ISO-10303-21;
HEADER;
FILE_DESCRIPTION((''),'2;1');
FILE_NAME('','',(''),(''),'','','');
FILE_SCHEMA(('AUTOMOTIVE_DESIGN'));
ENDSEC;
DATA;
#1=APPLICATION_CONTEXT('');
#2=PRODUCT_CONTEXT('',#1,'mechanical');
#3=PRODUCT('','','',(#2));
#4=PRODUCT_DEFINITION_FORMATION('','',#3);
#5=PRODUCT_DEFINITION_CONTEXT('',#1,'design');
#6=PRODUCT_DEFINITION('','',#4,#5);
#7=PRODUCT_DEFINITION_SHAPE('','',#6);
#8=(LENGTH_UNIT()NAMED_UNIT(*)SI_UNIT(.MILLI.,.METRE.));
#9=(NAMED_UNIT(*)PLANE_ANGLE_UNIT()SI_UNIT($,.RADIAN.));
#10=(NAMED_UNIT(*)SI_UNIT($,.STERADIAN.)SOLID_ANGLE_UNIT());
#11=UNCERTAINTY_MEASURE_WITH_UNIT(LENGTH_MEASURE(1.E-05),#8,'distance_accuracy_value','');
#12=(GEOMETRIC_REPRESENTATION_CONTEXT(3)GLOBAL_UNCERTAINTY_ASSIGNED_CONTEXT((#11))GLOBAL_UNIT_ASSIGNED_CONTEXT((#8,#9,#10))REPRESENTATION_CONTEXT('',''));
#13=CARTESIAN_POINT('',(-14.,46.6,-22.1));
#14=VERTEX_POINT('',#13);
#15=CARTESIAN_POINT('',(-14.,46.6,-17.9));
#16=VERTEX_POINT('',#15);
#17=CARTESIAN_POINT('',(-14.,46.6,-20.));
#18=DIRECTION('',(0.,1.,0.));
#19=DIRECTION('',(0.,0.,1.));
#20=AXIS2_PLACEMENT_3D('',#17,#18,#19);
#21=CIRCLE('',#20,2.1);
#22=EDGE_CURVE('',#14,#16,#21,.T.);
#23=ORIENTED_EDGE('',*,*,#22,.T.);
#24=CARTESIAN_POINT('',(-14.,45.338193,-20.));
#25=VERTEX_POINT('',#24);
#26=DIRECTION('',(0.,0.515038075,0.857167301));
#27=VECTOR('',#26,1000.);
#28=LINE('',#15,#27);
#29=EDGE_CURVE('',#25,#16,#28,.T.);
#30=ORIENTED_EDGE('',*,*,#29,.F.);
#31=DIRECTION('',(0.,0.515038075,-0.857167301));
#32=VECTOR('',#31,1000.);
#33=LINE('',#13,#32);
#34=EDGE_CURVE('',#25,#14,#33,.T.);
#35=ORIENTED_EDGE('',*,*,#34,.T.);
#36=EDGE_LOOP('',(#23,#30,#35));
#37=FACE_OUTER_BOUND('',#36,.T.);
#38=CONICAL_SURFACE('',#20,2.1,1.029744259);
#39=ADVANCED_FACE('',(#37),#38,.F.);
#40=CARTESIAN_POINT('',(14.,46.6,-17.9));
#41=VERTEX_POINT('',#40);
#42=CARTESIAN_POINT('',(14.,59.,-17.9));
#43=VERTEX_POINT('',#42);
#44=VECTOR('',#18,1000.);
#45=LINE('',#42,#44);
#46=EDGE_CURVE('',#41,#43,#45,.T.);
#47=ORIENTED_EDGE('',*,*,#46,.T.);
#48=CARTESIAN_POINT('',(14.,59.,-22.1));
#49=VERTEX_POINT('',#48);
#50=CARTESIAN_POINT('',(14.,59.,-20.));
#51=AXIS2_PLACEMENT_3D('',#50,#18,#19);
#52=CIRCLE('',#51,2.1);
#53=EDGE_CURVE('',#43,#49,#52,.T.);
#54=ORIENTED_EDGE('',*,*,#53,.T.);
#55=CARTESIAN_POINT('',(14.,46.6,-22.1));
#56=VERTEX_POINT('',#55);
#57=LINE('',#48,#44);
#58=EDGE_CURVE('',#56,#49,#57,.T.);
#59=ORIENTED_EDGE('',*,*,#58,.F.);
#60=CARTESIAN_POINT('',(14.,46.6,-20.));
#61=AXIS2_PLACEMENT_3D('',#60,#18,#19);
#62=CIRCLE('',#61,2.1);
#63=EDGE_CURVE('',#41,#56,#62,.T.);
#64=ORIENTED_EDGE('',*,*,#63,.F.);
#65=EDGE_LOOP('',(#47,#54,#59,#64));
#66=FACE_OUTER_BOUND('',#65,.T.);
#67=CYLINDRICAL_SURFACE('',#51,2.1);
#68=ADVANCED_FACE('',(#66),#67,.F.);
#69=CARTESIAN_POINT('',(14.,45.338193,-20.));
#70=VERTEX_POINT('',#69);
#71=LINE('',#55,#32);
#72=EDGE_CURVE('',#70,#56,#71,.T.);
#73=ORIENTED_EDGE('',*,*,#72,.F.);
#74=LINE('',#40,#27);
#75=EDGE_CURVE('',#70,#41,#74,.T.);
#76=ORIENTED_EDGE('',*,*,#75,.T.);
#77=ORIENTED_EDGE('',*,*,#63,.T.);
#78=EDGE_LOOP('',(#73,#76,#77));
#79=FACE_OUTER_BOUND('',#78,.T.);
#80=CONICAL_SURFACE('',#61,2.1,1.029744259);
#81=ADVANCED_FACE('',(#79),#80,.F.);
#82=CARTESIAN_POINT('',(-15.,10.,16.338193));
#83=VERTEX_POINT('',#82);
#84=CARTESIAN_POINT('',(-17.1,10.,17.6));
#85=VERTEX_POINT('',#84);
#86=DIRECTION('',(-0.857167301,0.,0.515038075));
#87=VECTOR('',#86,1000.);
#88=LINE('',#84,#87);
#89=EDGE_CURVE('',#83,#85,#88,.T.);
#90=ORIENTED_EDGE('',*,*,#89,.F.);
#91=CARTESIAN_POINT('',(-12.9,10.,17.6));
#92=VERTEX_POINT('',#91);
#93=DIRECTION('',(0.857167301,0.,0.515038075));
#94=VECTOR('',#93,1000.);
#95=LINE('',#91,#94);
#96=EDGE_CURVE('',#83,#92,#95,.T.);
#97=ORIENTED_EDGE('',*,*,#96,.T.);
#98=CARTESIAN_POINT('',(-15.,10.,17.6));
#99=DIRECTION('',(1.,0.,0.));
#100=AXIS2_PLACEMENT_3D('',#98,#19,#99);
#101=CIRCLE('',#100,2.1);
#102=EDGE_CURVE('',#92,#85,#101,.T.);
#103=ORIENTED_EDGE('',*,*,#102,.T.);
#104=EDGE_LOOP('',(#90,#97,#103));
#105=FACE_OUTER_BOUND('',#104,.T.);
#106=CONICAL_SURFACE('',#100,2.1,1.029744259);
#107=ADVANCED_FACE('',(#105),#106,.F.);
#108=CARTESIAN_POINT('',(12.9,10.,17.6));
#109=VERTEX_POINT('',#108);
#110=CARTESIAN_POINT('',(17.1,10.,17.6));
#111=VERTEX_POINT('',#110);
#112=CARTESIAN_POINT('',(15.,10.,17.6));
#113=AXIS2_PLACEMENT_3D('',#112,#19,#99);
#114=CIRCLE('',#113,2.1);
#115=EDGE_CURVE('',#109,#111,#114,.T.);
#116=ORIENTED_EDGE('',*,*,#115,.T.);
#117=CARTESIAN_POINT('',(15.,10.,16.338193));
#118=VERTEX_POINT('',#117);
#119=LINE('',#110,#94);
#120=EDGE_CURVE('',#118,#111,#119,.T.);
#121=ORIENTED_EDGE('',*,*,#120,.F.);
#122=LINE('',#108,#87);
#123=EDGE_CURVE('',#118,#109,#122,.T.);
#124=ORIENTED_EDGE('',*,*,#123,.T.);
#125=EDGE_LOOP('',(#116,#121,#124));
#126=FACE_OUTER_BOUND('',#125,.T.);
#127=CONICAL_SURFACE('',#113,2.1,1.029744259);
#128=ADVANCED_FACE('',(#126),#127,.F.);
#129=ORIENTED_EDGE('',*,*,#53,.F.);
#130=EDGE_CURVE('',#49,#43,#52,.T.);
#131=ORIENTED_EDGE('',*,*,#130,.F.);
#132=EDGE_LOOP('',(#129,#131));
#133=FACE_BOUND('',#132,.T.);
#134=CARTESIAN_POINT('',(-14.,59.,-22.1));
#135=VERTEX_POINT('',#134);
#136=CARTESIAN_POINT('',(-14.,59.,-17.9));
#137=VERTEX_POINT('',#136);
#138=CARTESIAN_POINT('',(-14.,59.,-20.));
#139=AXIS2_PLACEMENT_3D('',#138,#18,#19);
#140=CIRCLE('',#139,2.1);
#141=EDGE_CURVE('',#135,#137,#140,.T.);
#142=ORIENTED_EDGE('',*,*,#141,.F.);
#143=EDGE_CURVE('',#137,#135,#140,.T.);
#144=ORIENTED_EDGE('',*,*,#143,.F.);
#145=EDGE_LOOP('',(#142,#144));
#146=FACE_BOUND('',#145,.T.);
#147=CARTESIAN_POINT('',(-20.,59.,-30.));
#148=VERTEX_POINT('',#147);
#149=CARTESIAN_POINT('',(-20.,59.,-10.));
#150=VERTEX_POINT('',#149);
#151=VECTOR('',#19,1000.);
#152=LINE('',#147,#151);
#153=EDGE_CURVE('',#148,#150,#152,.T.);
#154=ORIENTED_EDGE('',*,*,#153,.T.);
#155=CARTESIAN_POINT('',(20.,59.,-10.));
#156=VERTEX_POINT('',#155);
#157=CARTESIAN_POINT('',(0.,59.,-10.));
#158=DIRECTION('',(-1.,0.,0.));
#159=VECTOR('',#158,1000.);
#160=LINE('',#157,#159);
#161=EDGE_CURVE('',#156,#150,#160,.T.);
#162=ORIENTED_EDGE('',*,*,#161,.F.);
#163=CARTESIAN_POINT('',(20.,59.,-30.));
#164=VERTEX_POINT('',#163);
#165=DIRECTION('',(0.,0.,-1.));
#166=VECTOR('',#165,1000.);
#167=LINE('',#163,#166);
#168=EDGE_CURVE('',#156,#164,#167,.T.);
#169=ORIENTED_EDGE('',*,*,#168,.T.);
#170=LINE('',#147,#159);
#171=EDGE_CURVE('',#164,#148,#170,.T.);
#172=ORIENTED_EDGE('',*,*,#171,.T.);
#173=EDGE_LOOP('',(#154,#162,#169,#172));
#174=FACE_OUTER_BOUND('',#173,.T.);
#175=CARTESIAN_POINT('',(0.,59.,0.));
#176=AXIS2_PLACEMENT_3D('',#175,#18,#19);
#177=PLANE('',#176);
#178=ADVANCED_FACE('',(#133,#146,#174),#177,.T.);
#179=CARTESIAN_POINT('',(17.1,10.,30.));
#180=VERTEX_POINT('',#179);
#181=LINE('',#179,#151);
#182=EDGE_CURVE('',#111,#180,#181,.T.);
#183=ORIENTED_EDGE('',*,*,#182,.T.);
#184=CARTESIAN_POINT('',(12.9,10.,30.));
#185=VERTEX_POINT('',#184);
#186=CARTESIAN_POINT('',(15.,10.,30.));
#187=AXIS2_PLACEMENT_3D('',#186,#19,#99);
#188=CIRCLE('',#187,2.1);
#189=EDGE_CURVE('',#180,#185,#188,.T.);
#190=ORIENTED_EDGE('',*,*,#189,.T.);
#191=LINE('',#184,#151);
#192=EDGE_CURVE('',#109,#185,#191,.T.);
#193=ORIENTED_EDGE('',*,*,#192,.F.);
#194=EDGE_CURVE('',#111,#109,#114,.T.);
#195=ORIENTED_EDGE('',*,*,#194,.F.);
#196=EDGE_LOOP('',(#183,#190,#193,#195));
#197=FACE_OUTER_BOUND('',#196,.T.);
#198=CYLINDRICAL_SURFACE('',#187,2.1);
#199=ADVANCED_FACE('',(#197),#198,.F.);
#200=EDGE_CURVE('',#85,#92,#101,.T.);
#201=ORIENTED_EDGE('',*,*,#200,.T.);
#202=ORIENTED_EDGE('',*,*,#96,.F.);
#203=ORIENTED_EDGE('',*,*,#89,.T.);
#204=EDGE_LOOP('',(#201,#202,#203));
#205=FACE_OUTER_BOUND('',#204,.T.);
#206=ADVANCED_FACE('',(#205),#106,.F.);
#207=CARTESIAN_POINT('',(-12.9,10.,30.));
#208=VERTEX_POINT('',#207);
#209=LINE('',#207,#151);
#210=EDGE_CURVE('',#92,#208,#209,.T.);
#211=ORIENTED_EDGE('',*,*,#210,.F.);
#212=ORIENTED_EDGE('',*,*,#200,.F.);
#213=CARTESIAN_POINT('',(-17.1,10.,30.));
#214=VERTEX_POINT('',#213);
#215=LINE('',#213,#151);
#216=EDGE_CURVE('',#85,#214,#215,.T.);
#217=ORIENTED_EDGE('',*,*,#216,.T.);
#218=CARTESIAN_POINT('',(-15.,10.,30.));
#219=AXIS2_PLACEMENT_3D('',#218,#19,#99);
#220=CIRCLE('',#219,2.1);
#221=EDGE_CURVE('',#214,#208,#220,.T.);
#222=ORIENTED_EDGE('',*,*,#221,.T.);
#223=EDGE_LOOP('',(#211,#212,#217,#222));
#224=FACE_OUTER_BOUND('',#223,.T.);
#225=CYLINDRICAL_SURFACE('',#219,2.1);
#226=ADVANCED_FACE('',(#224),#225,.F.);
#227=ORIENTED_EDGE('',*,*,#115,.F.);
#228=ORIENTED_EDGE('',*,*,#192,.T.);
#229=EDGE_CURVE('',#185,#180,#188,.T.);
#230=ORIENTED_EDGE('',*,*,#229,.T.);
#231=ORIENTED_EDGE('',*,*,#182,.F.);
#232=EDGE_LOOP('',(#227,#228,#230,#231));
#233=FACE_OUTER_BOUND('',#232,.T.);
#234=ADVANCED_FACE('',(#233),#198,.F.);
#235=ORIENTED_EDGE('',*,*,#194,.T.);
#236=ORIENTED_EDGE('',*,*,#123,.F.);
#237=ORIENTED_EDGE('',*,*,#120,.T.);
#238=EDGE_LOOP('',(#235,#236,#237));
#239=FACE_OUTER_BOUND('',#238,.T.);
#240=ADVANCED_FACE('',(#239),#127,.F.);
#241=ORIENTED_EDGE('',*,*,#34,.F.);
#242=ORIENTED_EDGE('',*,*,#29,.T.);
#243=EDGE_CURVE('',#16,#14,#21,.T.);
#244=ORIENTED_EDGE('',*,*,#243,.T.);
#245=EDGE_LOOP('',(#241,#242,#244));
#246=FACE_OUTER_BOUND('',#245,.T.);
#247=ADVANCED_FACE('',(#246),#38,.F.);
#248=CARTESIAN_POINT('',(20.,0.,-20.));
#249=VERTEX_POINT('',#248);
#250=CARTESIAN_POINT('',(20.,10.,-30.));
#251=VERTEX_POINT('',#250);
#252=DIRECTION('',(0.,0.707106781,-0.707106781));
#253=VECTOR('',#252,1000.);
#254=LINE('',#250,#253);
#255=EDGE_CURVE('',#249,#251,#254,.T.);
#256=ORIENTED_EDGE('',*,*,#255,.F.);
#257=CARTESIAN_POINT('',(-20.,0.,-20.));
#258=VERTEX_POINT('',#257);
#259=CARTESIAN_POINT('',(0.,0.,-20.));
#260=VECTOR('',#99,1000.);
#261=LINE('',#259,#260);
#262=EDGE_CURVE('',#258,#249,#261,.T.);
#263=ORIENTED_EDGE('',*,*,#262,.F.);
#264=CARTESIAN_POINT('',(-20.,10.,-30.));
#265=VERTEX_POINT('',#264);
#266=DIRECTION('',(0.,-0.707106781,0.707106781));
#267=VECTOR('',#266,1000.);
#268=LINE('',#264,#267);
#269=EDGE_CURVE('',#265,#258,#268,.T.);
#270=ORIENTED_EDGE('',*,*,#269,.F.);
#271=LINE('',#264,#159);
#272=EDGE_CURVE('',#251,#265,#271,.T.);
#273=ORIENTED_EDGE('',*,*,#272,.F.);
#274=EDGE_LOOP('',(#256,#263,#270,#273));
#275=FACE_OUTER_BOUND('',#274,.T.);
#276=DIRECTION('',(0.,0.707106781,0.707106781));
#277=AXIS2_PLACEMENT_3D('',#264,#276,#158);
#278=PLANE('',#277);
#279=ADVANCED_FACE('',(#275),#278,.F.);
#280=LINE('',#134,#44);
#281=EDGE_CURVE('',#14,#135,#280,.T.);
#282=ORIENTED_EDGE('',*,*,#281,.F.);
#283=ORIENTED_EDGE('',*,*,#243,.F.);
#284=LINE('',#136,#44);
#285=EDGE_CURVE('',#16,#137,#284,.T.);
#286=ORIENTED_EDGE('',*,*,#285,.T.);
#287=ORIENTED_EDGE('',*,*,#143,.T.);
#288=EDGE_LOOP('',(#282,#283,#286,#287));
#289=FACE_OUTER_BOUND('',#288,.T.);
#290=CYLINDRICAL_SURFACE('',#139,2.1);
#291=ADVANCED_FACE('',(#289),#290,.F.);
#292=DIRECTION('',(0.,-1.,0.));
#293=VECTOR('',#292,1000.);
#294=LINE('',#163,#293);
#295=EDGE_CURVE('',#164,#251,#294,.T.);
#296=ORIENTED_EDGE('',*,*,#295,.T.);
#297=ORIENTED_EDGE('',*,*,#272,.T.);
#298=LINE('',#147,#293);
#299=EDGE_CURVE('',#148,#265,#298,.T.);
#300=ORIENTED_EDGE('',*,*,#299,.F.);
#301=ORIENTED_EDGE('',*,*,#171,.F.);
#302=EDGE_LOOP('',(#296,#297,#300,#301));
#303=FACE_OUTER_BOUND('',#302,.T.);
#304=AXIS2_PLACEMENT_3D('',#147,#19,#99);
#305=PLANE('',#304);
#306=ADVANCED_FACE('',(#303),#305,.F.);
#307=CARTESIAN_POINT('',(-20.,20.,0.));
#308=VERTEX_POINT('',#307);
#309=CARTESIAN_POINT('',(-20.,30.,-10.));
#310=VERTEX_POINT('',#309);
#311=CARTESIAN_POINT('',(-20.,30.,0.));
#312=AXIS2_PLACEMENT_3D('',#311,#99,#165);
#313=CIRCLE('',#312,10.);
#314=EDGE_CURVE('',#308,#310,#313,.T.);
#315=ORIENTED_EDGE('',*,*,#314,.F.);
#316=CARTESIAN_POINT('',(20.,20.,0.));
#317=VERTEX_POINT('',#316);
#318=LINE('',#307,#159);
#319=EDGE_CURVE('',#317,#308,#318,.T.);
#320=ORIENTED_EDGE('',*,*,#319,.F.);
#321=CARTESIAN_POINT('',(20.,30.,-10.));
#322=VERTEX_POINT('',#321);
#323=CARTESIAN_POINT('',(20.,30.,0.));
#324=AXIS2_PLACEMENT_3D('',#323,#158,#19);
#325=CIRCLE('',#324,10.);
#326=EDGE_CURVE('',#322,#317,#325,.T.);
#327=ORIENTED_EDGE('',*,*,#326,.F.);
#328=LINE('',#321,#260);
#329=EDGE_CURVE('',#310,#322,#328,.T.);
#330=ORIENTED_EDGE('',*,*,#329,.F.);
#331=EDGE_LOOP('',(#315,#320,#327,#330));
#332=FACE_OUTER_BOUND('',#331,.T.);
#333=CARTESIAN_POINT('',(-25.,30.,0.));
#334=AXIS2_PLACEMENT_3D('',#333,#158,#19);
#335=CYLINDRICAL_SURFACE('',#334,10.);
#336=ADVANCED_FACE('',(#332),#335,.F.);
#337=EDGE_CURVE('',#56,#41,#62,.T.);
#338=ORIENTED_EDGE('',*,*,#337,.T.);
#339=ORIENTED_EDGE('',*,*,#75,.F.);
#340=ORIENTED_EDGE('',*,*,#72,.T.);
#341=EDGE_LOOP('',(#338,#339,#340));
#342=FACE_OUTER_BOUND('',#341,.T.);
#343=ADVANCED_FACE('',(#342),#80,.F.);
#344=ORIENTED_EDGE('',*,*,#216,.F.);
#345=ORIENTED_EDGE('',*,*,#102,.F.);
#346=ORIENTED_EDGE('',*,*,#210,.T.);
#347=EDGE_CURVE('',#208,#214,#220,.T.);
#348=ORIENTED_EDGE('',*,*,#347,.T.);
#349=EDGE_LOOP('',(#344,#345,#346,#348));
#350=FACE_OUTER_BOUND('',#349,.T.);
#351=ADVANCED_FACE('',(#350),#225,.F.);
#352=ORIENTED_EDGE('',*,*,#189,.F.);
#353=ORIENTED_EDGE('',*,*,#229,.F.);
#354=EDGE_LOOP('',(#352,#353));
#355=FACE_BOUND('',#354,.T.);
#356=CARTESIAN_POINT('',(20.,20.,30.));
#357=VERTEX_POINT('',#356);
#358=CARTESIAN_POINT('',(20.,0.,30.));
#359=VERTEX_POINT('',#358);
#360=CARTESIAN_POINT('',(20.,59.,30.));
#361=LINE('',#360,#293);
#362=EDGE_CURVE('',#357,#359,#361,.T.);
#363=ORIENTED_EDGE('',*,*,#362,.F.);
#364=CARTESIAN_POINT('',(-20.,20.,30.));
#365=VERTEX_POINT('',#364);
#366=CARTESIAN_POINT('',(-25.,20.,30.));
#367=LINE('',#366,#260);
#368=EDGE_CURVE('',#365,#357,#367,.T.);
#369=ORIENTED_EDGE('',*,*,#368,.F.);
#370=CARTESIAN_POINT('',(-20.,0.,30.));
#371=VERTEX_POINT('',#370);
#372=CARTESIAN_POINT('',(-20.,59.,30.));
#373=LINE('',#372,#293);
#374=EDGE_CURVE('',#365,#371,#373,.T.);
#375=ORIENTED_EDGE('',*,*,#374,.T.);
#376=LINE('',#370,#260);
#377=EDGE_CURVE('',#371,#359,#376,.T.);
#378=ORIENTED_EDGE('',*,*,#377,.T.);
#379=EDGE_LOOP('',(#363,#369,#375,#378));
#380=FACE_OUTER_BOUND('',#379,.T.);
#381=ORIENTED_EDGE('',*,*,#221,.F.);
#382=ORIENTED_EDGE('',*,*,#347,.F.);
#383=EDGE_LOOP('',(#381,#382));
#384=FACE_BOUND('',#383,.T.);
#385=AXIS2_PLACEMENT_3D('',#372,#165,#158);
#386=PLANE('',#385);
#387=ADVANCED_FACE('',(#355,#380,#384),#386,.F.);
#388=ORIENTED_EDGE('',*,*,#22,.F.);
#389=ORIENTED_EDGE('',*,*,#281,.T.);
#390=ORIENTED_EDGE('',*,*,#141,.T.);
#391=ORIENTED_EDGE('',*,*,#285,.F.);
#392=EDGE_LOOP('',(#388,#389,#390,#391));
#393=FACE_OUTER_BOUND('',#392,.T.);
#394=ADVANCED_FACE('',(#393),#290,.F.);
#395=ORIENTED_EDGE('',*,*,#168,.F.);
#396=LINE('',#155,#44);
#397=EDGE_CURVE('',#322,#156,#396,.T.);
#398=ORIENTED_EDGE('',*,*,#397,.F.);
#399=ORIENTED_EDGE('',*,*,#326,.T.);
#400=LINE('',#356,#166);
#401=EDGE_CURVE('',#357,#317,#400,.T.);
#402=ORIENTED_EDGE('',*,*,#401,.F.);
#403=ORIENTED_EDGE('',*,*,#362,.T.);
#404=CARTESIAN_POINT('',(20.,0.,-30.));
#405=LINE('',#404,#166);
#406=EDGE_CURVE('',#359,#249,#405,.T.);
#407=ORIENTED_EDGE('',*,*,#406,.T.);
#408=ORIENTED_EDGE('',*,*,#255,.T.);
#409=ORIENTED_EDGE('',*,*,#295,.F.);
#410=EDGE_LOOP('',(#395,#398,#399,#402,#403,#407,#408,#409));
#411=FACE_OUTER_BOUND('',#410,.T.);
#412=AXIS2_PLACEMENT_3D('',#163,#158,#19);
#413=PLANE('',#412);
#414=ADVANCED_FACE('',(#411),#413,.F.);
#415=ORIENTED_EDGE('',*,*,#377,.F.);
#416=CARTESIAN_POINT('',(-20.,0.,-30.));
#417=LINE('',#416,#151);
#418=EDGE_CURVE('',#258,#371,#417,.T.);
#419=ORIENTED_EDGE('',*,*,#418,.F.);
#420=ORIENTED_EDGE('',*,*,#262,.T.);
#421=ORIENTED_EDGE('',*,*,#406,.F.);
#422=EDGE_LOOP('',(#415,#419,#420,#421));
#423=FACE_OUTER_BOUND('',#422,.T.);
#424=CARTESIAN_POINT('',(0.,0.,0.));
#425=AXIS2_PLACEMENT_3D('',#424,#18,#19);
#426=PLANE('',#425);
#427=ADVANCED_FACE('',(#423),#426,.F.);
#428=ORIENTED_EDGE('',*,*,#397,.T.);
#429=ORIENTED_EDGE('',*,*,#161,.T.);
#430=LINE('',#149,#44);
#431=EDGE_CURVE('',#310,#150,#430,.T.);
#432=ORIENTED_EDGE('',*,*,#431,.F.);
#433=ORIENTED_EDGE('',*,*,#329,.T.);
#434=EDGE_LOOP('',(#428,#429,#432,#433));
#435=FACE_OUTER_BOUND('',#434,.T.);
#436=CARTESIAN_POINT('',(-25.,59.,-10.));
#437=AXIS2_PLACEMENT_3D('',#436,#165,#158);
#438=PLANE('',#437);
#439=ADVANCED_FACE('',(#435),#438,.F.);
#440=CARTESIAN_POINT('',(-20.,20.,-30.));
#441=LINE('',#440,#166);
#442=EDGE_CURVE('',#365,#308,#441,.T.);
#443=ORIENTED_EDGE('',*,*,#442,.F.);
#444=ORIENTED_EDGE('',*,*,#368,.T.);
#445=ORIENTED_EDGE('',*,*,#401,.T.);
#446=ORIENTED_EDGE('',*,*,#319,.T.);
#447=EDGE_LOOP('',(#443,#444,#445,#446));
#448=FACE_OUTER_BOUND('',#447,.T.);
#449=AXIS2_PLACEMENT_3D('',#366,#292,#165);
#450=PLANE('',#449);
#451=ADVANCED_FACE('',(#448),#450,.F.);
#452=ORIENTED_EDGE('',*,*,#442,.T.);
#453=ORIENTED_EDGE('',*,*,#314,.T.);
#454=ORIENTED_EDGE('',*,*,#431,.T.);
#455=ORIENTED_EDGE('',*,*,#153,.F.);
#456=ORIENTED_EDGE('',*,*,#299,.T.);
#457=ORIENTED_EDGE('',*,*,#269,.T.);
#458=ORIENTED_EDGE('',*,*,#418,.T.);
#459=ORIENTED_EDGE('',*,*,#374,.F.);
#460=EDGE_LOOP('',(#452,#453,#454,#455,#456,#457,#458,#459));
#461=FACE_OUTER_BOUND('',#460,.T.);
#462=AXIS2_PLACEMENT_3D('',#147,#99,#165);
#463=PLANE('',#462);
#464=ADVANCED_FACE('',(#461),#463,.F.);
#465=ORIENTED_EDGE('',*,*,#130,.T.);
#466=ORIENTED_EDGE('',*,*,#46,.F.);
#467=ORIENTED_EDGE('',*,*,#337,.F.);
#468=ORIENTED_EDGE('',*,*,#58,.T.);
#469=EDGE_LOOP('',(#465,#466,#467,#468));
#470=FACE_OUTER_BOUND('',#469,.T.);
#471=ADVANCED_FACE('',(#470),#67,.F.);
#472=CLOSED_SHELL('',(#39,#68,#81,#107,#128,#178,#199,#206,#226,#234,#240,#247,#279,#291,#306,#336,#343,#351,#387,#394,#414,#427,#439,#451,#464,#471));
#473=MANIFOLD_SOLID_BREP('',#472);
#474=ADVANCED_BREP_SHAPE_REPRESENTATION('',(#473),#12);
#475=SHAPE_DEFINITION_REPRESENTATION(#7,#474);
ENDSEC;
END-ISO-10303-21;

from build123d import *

# Parameters (mm, degrees)
SKETCH1_W             = 40
SKETCH1_H             = 60
BOSS_EXTRUDE1_DEPTH   = 59
SKETCH2_W             = 40
SKETCH2_H             = 39
CUT_EXTRUDE1_DEPTH    = 45
CHAMFER1_SIZE         = 10
FILLET1_R             = 10
M5_TAPPED_HOLE1_D     = 4.2
M5_TAPPED_HOLE1_DEPTH = 12.4
M5_TAPPED_HOLE1_TIP   = 1.2618073
M5_TAPPED_HOLE2_D     = 4.2
M5_TAPPED_HOLE2_DEPTH = 12.4
M5_TAPPED_HOLE2_TIP   = 1.2618073


with BuildPart() as part:
    # Sketch1 → Boss-Extrude1 (new body)
    with BuildSketch(Plane(origin=(0, 0, 0), x_dir=(1, 0, 0), z_dir=(0, 1, 0))):
        Rectangle(SKETCH1_W, SKETCH1_H)
    extrude(amount=BOSS_EXTRUDE1_DEPTH)

    # Sketch2 → Cut-Extrude1 (cut)
    with BuildSketch(Plane(origin=(20, 0, 0), x_dir=(0, 0, -1), z_dir=(1, 0, 0))):
        with Locations((-10, 39.5)):
            Rectangle(SKETCH2_W, SKETCH2_H)
    extrude(amount=-CUT_EXTRUDE1_DEPTH, mode=Mode.SUBTRACT)

    # Chamfer1
    chamfer1_edges = [part.edges().sort_by_distance(p)[0] for p in [
        (0, 0, -30),
    ]]
    chamfer(chamfer1_edges, length=CHAMFER1_SIZE)

    # Fillet1
    fillet1_edges = [part.edges().sort_by_distance(p)[0] for p in [
        (0, 20, -10),
    ]]
    fillet(fillet1_edges, radius=FILLET1_R)

    # M5 Tapped Hole1
    with Locations(Plane(origin=(-14, 59, -20), x_dir=(0, 0, 1), z_dir=(0, 1, 0))):
        with Locations((0, 0), (0, 28)):
            Hole(M5_TAPPED_HOLE1_D / 2, depth=M5_TAPPED_HOLE1_DEPTH)
            with Locations((0, 0, -(M5_TAPPED_HOLE1_DEPTH + M5_TAPPED_HOLE1_TIP / 2))):  # 118° drill point
                Cone(0, M5_TAPPED_HOLE1_D / 2, M5_TAPPED_HOLE1_TIP, mode=Mode.SUBTRACT)

    # M5 Tapped Hole2
    with Locations(Plane(origin=(-15, 10, 30), x_dir=(1, 0, 0), z_dir=(0, 0, 1))):
        with Locations((0, 0), (30, 0)):
            Hole(M5_TAPPED_HOLE2_D / 2, depth=M5_TAPPED_HOLE2_DEPTH)
            with Locations((0, 0, -(M5_TAPPED_HOLE2_DEPTH + M5_TAPPED_HOLE2_TIP / 2))):  # 118° drill point
                Cone(0, M5_TAPPED_HOLE2_D / 2, M5_TAPPED_HOLE2_TIP, mode=Mode.SUBTRACT)


solid = part.part
